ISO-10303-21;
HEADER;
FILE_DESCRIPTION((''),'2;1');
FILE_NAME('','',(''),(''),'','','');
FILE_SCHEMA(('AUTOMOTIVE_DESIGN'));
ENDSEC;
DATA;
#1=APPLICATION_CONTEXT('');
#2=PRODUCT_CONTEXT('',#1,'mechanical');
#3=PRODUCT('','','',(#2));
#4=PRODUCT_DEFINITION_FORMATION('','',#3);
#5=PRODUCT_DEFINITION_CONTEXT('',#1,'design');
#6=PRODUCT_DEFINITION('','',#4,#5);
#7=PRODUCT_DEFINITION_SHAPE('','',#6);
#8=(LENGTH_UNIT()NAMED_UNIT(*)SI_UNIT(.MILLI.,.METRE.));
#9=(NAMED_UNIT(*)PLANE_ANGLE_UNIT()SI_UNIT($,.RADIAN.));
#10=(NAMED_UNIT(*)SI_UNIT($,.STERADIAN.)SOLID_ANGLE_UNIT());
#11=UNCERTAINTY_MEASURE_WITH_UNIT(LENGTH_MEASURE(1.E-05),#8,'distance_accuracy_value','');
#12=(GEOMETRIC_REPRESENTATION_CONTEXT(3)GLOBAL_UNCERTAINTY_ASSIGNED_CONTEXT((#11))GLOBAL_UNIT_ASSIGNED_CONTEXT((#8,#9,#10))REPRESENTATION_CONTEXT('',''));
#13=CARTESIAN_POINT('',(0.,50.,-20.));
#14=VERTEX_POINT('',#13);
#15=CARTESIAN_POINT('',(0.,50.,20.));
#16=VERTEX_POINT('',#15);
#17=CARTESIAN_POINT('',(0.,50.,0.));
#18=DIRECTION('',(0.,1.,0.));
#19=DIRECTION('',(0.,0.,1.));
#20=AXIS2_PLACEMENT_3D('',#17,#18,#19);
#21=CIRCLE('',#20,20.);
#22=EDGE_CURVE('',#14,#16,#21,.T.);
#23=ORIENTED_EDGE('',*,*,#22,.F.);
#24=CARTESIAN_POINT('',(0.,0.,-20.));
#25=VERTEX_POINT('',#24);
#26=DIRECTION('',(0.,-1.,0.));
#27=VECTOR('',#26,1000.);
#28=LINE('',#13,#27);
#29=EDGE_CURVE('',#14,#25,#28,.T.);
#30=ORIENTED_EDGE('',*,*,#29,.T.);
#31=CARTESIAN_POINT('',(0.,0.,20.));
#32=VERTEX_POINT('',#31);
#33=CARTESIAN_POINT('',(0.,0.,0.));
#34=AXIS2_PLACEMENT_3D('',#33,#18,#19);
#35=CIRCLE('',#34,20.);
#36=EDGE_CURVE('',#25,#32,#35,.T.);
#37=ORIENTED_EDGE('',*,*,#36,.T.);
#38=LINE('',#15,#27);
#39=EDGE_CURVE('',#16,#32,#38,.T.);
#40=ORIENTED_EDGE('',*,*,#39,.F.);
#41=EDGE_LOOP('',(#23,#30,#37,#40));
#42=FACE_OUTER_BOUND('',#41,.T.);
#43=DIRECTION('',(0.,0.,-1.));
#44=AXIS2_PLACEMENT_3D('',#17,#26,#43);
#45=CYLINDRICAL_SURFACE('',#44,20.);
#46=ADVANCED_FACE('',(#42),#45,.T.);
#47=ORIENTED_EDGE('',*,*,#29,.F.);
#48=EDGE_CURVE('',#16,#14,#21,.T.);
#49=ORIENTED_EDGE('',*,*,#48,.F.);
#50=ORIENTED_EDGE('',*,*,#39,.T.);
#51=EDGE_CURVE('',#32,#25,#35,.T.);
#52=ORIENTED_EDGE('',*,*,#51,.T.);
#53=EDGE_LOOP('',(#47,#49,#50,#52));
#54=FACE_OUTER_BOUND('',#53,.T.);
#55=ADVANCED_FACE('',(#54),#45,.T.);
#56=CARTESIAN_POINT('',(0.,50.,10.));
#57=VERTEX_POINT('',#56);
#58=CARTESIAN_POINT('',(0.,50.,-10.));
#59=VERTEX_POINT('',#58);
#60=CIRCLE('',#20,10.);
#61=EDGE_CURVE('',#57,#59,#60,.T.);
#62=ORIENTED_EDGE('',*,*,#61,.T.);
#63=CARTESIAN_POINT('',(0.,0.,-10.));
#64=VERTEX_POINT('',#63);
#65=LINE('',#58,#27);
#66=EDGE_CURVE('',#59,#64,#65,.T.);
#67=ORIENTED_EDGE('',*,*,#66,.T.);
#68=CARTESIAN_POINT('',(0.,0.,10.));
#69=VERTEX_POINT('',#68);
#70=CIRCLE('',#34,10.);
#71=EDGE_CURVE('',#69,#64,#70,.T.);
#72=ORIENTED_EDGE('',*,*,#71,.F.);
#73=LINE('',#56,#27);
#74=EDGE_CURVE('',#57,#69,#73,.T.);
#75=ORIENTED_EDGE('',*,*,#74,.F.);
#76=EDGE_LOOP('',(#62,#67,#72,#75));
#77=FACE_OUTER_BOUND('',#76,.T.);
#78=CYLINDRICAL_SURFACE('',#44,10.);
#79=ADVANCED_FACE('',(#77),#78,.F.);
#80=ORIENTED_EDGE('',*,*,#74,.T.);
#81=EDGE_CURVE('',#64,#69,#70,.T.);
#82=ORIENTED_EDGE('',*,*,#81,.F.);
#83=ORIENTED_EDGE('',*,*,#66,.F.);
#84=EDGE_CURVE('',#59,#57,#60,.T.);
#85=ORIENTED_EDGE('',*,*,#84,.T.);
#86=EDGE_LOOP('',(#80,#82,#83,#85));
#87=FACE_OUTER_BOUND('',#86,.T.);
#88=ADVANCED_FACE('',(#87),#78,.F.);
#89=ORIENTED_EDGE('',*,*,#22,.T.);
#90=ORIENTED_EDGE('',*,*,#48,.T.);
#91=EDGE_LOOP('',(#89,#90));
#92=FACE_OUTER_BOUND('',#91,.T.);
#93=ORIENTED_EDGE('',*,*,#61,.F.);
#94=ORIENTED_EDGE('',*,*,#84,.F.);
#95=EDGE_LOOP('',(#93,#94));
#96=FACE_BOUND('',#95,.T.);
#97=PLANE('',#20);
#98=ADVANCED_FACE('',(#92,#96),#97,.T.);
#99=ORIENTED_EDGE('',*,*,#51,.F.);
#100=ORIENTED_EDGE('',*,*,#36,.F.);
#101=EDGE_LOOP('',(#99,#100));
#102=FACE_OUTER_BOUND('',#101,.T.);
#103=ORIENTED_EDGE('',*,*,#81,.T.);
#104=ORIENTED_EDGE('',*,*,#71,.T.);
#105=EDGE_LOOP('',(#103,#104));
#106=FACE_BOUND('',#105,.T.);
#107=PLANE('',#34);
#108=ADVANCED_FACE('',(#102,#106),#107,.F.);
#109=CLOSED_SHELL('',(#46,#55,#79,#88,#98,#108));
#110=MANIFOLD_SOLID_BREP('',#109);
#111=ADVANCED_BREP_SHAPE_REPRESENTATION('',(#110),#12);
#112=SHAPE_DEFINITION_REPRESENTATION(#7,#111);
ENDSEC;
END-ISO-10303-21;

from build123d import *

# Parameters (mm, degrees)
SKETCH1_R           = 20
SKETCH1_R_2         = 10
BOSS_EXTRUDE1_DEPTH = 50


with BuildPart() as part:
    # Sketch1 → Boss-Extrude1 (new body)
    with BuildSketch(Plane(origin=(0, 0, 0), x_dir=(1, 0, 0), z_dir=(0, 1, 0))):
        with Locations(Location((0, 0, 0), (0, 0, 270))):
            Circle(SKETCH1_R)
        with Locations(Location((0, 0, 0), (0, 0, 270))):
            Circle(SKETCH1_R_2, mode=Mode.SUBTRACT)
    extrude(amount=BOSS_EXTRUDE1_DEPTH)


solid = part.part
